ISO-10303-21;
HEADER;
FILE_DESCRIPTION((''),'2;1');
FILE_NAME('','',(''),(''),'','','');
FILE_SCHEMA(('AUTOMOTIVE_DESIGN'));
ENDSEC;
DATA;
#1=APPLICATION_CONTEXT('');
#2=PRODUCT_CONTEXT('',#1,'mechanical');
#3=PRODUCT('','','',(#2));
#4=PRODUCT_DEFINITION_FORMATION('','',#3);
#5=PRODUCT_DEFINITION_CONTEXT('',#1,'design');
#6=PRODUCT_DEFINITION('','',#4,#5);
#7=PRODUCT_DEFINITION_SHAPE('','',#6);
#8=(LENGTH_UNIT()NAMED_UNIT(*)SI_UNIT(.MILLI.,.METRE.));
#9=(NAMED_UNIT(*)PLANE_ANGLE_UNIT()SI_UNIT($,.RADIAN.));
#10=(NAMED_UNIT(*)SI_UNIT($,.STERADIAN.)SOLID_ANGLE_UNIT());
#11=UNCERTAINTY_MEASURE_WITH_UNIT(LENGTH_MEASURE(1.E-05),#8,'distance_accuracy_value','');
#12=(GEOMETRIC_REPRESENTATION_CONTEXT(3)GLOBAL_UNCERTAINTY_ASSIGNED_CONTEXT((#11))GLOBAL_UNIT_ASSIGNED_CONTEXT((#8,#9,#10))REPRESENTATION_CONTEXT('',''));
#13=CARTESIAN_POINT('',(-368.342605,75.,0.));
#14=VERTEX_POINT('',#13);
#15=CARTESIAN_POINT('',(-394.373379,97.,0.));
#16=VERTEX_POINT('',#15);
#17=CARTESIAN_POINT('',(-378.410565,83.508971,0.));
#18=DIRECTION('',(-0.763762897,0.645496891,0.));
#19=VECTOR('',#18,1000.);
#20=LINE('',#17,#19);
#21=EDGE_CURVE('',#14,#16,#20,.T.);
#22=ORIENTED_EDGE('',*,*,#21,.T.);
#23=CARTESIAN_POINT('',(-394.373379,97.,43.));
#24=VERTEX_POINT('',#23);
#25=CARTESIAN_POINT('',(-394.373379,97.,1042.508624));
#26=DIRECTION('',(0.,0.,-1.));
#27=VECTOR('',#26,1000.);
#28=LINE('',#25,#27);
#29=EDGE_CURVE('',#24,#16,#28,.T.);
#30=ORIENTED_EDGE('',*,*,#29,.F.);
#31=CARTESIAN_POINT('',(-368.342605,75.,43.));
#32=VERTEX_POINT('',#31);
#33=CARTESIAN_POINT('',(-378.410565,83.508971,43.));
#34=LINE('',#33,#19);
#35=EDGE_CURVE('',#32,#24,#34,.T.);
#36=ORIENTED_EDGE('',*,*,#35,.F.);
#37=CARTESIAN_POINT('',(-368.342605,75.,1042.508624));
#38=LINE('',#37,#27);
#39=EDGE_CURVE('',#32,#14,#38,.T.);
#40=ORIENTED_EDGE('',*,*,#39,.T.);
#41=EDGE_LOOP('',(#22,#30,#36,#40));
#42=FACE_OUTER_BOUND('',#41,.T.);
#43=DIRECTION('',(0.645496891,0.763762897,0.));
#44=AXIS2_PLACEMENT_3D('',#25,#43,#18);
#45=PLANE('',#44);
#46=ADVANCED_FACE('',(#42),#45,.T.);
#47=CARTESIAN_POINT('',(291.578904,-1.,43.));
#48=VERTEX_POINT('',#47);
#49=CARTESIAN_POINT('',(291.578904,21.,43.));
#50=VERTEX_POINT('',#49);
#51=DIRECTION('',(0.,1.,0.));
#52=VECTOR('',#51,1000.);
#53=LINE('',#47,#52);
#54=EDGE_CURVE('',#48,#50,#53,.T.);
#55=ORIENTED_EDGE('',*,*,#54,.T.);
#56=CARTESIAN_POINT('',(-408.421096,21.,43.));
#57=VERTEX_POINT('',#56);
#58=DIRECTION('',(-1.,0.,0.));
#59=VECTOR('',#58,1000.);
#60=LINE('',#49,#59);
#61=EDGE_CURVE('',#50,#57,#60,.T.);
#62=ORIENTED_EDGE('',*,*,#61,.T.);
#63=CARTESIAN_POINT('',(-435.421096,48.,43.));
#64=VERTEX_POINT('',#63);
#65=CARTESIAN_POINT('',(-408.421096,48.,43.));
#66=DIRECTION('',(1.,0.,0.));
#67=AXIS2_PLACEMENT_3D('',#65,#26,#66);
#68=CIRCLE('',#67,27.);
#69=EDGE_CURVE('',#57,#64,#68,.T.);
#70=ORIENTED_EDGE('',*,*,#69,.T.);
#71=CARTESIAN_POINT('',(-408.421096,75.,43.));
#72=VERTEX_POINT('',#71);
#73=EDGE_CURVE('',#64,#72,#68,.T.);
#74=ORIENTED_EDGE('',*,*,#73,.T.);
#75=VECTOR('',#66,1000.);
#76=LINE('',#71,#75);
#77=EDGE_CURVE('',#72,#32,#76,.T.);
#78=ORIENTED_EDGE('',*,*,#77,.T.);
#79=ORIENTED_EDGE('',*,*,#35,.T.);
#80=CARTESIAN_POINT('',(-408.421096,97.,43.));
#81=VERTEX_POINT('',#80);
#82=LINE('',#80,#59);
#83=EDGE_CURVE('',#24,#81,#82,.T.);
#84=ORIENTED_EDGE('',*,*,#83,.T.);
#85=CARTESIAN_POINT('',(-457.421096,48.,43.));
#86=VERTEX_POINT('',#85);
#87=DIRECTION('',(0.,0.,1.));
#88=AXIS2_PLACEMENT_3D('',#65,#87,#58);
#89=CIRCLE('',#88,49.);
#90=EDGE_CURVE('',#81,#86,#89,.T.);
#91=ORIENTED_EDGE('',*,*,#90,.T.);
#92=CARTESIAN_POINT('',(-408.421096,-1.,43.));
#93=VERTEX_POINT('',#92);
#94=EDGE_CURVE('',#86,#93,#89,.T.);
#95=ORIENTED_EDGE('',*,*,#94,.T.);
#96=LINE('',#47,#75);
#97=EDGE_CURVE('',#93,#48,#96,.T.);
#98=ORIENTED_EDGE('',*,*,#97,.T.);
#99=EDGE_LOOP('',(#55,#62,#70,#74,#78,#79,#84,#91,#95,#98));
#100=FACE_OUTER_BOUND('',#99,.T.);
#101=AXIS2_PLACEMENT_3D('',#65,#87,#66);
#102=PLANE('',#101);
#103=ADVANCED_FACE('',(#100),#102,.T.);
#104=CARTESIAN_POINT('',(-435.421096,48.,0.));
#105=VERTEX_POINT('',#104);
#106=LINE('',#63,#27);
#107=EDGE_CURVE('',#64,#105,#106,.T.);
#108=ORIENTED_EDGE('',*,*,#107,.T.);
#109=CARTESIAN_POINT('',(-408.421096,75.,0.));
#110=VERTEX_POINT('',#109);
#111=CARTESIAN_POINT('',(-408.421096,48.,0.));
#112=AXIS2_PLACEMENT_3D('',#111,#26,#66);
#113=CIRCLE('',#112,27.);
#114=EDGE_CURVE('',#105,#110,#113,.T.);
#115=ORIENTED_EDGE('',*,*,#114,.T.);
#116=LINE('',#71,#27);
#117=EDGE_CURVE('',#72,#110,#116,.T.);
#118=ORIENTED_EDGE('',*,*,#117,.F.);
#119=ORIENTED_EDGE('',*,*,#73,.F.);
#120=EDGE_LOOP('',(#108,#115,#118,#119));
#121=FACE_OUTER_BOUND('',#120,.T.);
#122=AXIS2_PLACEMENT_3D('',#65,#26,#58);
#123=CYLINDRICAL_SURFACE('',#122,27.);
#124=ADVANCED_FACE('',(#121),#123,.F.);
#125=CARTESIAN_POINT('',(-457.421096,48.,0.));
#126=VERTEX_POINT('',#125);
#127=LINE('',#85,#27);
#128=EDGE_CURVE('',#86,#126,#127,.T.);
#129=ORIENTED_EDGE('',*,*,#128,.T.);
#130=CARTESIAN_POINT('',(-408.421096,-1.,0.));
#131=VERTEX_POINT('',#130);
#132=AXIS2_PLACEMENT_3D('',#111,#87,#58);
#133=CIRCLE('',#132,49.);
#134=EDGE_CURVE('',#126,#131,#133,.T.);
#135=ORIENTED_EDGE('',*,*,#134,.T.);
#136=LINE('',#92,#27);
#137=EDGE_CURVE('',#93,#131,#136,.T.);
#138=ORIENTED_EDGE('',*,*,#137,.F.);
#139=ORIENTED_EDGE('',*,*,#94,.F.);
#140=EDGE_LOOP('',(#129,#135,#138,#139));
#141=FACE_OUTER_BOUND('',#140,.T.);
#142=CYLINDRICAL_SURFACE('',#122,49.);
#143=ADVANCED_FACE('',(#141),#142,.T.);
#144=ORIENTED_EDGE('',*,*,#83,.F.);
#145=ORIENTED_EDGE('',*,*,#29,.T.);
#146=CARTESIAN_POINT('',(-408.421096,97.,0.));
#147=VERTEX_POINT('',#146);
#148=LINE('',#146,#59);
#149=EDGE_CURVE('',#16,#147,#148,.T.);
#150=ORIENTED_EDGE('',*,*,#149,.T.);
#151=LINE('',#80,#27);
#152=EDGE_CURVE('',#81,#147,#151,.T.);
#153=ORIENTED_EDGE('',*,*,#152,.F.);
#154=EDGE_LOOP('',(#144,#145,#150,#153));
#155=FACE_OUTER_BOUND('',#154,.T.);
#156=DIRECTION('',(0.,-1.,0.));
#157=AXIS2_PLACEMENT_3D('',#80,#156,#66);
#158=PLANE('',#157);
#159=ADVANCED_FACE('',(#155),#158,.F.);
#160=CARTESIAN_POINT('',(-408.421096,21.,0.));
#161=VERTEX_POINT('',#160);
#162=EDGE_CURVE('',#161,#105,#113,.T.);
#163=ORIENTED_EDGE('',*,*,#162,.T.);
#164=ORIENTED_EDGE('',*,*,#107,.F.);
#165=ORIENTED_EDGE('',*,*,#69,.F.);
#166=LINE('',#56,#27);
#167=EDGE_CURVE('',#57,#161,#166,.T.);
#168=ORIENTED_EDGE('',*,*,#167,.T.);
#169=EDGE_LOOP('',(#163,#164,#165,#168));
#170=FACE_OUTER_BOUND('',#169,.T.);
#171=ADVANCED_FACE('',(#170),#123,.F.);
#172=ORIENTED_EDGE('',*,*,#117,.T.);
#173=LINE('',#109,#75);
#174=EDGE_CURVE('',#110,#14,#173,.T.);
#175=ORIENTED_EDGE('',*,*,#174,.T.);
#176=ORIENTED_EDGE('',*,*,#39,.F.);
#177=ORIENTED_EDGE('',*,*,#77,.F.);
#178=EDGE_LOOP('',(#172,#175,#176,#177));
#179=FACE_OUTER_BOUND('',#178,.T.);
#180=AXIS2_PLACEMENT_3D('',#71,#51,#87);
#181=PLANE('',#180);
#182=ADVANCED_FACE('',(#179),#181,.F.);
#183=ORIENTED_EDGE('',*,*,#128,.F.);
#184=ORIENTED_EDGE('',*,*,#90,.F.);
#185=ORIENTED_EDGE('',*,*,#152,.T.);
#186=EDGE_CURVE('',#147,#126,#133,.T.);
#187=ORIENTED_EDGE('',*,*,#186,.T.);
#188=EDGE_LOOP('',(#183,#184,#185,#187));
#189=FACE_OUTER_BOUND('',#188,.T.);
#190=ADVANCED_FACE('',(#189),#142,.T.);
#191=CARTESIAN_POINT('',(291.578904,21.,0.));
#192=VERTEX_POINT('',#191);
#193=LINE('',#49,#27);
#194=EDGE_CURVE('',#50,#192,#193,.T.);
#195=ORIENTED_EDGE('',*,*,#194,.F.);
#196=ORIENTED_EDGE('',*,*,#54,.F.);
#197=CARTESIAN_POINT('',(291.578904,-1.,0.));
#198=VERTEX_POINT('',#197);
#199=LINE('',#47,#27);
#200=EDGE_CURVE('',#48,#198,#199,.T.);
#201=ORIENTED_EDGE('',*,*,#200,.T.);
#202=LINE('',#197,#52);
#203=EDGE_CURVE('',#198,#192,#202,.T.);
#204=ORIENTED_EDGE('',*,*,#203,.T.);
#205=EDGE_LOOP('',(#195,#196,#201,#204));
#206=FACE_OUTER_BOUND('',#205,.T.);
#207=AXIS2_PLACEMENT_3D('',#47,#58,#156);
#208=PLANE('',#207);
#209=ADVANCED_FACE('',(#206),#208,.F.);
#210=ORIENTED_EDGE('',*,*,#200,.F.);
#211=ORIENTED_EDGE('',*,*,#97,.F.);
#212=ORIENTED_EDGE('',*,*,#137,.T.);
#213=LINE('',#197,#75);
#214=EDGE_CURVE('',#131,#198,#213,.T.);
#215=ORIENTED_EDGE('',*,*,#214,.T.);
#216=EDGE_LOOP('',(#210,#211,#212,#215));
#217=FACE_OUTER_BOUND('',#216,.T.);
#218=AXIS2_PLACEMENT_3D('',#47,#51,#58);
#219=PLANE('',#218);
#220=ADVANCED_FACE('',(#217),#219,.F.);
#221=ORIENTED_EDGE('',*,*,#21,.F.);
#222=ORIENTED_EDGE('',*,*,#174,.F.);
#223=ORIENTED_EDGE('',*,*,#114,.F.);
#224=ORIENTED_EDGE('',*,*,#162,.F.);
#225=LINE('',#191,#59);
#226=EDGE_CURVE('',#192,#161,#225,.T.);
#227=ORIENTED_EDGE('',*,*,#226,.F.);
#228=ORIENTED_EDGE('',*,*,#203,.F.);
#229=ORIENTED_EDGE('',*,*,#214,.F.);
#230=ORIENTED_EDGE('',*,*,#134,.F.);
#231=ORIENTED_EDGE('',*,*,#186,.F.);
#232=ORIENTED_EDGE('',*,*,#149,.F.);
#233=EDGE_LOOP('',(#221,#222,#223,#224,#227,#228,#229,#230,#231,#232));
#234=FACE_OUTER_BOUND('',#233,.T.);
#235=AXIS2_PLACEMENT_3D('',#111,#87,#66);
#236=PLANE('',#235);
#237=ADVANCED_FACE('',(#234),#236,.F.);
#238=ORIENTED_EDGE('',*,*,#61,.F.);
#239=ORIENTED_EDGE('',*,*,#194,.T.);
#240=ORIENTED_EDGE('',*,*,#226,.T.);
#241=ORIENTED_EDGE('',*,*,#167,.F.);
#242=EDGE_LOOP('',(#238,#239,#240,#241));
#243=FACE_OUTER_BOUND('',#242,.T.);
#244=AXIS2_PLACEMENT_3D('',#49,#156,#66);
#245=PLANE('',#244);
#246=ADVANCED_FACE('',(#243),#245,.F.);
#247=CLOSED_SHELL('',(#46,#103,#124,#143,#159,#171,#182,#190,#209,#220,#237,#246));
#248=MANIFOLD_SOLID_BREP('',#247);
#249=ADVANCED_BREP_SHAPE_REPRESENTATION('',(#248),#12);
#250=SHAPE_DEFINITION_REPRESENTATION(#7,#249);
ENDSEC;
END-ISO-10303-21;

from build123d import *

# Parameters (mm, degrees)
EXTRUDE_1_DEPTH          = 43
CUT_EXTRUDE_1_DEPTH      = 470.565819802
CUT_EXTRUDE_1_DEPTH_BACK = 470.565819802


with BuildPart() as part:
    # 草图1 → 凸台-拉伸1 (new body)
    with BuildSketch(Plane.XY):
        with BuildLine():
            Line((291.578903934, -1), (-408.421096066, -1))
            ThreePointArc((-408.421096066, -1), (-457.421096066, 48), (-408.421096066, 97))
            Line((-408.421096066, 97), (-357.864757467, 97))
            Line((-357.864757467, 97), (-315.394306565, 75))
            Line((-315.394306565, 75), (-408.421096066, 75))
            ThreePointArc((-408.421096066, 75), (-435.421096066, 48), (-408.421096066, 21))
            Line((-408.421096066, 21), (291.578903934, 21))
            Line((291.578903934, 21), (291.578903934, -1))
        make_face()
    extrude(amount=EXTRUDE_1_DEPTH)

    # 草图2 → 切除-拉伸1 (cut, two sides: drawn at the far end of the back side and taken through both)
    with BuildSketch(Plane.XY.offset(43).offset(-CUT_EXTRUDE_1_DEPTH_BACK)):
        Polygon((-357.864757467, 97), (-394.373379174, 97), (-368.3426051, 75), (-315.394306565, 75), align=None)
    extrude(amount=CUT_EXTRUDE_1_DEPTH + CUT_EXTRUDE_1_DEPTH_BACK, mode=Mode.SUBTRACT)


solid = part.part
